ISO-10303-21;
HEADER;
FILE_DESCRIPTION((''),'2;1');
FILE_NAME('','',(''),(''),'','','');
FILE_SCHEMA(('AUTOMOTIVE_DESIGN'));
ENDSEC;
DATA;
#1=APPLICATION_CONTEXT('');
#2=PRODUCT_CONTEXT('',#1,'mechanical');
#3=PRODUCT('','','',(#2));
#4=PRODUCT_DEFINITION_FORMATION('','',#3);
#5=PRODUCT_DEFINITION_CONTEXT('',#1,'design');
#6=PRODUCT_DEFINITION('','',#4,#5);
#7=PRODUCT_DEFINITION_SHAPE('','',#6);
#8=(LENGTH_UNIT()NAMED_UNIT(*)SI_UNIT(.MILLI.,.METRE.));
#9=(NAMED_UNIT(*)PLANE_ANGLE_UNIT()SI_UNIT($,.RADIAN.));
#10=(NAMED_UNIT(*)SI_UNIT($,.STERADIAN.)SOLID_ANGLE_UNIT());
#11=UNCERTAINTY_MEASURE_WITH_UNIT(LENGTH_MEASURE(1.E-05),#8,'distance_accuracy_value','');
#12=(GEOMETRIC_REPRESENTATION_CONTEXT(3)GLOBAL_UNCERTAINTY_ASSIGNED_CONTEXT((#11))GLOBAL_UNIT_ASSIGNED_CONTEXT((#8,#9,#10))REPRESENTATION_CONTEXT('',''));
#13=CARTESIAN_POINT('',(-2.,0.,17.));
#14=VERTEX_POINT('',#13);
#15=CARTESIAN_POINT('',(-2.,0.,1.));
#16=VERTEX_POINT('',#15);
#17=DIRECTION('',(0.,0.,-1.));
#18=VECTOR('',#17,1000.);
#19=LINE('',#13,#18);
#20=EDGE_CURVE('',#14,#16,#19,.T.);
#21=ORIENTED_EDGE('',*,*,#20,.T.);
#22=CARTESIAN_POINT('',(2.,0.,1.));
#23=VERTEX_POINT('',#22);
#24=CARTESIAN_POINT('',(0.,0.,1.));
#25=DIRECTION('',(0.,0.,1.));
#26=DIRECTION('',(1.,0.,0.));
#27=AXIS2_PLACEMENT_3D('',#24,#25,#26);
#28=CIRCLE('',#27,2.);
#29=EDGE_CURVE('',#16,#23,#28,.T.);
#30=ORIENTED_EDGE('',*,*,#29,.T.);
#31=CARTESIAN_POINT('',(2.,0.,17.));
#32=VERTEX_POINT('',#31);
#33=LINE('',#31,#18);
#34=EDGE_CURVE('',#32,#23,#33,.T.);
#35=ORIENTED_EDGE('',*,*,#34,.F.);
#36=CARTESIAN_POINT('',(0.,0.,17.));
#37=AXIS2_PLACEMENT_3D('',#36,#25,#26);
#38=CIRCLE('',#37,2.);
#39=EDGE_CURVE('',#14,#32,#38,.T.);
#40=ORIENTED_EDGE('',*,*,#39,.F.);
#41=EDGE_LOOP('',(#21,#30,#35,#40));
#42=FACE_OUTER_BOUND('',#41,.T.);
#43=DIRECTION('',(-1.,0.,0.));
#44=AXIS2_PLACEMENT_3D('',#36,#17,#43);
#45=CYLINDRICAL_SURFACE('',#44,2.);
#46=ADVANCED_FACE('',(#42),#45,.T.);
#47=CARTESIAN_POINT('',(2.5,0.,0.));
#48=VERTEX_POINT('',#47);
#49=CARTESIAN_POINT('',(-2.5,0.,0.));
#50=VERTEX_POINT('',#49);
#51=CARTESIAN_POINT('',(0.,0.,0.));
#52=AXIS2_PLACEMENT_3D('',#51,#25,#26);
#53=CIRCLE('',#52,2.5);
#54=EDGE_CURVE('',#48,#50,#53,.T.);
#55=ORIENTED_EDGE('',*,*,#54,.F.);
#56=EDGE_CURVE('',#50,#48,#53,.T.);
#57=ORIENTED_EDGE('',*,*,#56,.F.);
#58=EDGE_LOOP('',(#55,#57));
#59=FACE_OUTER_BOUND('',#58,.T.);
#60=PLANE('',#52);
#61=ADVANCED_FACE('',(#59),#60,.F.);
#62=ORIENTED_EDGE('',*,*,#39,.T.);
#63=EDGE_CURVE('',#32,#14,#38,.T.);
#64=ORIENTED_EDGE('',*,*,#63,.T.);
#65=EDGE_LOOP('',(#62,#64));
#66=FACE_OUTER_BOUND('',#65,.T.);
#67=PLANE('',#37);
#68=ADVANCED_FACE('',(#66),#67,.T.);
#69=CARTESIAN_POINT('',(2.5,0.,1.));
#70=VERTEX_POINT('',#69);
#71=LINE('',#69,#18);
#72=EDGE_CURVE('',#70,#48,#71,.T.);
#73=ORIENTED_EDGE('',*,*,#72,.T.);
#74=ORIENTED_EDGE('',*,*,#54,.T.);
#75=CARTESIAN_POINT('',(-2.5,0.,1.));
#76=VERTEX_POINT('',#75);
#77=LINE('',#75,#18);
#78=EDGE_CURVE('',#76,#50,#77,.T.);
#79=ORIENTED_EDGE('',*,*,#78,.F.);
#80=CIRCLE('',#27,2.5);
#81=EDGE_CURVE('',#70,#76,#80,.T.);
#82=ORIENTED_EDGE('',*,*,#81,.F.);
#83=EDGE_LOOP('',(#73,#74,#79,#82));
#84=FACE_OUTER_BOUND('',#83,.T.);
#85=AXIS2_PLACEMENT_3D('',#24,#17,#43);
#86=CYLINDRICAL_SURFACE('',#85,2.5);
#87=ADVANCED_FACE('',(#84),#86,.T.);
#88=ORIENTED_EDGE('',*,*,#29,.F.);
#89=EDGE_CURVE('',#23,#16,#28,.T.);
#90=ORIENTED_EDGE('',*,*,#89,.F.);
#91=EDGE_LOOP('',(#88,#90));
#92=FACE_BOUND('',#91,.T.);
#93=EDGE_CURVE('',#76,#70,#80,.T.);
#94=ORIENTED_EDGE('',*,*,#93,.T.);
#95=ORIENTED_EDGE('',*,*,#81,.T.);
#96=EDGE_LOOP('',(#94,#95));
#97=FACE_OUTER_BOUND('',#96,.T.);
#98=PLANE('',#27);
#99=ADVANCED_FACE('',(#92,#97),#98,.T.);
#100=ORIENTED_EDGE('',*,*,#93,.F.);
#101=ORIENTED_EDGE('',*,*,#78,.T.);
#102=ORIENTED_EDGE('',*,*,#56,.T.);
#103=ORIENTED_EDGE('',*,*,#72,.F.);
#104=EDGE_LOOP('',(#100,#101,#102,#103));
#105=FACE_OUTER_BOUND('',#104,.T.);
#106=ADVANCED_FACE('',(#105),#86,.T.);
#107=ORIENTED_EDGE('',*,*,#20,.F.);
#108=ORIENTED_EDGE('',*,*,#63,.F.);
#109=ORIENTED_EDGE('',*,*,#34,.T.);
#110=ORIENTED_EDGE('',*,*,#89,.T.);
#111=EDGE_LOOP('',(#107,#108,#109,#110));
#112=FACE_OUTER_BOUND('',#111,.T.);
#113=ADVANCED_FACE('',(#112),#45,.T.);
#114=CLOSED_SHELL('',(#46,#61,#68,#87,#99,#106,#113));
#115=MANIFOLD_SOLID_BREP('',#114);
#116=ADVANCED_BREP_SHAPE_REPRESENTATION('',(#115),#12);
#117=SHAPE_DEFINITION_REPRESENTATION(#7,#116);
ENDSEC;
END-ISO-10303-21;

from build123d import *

# Parameters (mm, degrees)
SKETCH_1_R      = 2.5
EXTRUDE_1_DEPTH = 1
SKETCH_2_R      = 2
EXTRUDE_2_DEPTH = 16


with BuildPart() as part:
    # 草图1 → 凸台-拉伸1 (new body)
    with BuildSketch(Plane.XY):
        Circle(SKETCH_1_R)
    extrude(amount=EXTRUDE_1_DEPTH)

    # 草图2 → 凸台-拉伸2 (add)
    with BuildSketch(Plane.XY.offset(1)):
        Circle(SKETCH_2_R)
    extrude(amount=EXTRUDE_2_DEPTH)


solid = part.part
